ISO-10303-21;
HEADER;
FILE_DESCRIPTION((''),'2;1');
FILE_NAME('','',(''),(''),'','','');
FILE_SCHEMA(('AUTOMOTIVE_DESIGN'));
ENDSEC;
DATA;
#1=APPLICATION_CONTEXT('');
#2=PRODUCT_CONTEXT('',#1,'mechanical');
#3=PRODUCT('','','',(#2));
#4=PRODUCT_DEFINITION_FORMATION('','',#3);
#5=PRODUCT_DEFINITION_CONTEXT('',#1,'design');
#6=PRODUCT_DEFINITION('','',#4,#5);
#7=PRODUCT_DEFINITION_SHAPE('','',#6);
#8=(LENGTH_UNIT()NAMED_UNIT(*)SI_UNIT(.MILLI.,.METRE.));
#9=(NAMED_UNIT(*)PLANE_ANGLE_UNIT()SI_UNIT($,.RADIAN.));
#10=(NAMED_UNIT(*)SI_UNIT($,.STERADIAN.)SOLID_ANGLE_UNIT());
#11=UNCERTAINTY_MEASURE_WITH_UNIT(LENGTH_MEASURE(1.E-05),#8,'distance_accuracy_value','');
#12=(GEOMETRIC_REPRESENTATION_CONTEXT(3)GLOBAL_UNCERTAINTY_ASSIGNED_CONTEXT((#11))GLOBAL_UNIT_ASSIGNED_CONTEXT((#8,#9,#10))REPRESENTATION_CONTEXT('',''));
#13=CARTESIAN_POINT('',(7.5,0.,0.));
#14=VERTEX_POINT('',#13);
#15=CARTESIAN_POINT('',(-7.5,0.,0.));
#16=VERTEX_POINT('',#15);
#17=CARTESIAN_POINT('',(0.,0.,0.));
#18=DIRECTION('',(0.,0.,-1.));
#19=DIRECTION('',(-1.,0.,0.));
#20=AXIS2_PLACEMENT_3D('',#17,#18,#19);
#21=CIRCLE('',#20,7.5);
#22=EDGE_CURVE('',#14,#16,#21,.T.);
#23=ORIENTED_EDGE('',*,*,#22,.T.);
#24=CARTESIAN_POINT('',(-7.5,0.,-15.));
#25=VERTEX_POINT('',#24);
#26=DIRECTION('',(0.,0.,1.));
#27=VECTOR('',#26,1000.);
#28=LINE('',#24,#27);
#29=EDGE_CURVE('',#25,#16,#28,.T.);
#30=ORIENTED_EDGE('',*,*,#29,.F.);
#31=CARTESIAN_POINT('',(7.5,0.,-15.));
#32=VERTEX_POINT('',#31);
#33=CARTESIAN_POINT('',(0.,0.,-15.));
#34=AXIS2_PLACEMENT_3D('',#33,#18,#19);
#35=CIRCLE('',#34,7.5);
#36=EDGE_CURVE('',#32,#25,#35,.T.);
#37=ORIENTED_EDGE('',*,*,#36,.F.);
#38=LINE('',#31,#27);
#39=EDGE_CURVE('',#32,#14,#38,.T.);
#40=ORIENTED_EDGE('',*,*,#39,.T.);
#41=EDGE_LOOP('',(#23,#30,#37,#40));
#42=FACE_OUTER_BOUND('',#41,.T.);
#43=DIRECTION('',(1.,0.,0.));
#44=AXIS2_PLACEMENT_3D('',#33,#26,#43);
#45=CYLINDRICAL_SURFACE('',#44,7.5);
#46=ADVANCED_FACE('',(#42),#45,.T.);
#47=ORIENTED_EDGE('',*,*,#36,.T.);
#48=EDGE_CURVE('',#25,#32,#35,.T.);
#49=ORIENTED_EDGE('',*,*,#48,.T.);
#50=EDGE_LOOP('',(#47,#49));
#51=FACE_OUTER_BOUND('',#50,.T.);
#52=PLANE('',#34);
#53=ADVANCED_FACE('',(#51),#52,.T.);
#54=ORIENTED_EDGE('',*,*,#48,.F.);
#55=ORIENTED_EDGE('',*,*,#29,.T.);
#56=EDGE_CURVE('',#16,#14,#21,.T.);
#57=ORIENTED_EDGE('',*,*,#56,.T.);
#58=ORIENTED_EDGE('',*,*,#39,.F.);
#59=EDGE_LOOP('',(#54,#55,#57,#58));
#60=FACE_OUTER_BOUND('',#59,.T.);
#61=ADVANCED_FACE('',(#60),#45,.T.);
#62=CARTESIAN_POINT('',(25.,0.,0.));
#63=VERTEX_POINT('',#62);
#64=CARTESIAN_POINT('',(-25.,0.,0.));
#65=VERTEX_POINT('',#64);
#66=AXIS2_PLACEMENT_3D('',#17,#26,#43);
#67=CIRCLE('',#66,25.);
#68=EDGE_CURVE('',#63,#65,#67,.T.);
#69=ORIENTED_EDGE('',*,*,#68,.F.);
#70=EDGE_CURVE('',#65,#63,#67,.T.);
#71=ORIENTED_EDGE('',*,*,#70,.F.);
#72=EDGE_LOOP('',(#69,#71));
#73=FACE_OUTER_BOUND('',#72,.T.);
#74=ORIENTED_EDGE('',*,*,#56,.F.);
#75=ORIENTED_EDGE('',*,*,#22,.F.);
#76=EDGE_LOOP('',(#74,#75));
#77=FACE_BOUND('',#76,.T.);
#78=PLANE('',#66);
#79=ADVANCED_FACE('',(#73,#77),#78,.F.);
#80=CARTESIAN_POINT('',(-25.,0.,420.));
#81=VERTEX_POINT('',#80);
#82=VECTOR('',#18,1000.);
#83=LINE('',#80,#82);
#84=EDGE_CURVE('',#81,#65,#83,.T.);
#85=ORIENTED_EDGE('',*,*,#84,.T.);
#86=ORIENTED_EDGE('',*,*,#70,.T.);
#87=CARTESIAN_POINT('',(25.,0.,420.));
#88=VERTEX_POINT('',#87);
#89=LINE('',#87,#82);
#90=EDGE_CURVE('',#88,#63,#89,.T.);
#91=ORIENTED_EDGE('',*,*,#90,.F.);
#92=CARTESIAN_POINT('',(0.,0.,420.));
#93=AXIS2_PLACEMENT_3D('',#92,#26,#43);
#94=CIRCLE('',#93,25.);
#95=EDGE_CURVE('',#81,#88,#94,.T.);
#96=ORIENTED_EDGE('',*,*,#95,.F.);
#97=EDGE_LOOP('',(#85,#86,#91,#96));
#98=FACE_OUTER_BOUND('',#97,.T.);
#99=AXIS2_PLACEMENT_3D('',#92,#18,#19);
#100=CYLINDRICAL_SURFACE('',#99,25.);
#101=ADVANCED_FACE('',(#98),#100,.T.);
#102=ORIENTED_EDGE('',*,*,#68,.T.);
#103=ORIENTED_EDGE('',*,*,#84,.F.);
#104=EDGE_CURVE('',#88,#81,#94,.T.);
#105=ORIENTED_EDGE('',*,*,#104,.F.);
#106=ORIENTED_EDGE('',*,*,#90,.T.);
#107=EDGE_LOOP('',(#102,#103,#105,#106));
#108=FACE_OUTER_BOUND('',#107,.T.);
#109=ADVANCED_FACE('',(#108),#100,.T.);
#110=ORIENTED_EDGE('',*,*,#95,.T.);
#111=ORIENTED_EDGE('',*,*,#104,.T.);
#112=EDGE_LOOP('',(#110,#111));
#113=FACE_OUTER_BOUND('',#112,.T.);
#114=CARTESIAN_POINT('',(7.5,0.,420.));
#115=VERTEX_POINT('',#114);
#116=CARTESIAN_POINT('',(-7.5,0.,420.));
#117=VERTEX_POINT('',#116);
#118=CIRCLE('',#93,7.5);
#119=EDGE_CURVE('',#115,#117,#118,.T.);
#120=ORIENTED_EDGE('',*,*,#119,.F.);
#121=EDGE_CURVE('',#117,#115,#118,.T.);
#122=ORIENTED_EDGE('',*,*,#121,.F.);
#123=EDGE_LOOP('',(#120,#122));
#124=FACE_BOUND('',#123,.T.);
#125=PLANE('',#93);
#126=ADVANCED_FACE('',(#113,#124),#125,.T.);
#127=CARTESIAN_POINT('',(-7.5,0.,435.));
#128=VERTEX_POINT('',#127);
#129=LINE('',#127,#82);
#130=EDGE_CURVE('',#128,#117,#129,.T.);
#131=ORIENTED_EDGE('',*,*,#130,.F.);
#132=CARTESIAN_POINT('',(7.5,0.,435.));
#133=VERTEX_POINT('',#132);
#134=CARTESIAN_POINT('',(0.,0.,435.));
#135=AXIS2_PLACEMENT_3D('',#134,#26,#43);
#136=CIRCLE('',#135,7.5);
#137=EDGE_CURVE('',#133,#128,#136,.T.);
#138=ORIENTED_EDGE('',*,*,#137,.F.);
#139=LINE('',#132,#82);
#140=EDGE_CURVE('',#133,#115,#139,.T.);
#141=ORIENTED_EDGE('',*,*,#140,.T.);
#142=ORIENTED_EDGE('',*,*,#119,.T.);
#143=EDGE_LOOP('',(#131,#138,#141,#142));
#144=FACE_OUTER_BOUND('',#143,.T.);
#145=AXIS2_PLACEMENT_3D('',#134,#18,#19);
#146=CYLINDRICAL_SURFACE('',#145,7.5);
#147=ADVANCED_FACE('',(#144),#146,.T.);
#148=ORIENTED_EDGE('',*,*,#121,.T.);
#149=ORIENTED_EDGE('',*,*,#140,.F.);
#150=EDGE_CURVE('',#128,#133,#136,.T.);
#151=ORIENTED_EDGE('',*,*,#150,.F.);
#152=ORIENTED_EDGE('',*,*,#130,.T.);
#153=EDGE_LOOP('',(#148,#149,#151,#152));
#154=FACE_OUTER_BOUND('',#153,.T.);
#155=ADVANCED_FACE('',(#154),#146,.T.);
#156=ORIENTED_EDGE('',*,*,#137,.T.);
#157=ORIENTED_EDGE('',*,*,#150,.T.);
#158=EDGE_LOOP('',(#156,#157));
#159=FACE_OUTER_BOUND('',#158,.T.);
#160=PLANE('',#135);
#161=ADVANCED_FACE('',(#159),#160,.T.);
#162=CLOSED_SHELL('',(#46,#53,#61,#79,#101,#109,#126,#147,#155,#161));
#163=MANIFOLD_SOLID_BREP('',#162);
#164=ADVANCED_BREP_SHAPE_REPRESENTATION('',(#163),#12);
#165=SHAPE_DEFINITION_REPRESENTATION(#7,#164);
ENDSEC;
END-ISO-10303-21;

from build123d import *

# Parameters (mm, degrees)
SKETCH_1_R      = 25
EXTRUDE_1_DEPTH = 420
SKETCH_2_R      = 7.5
EXTRUDE_2_DEPTH = 15
EXTRUDE_START   = 15
SKETCH_3_R      = 7.5
EXTRUDE_3_DEPTH = 15


with BuildPart() as part:
    # 草图1 → 凸台-拉伸1 (new body)
    with BuildSketch(Plane.XY):
        Circle(SKETCH_1_R)
    extrude(amount=EXTRUDE_1_DEPTH)

    # 草图2 → 凸台-拉伸2 (add)
    with BuildSketch(Plane.XY.offset(420)):
        Circle(SKETCH_2_R)
    extrude(amount=EXTRUDE_2_DEPTH)

    # 草图3 → 凸台-拉伸3 (add)
    with BuildSketch(Plane(origin=(0, 0, 0), x_dir=(-1, 0, 0), z_dir=(0, 0, -1)).offset(EXTRUDE_START)):
        with Locations(Location((0, 0, 0), (0, 0, 180))):
            Circle(SKETCH_3_R)
    extrude(amount=-EXTRUDE_3_DEPTH)


solid = part.part
